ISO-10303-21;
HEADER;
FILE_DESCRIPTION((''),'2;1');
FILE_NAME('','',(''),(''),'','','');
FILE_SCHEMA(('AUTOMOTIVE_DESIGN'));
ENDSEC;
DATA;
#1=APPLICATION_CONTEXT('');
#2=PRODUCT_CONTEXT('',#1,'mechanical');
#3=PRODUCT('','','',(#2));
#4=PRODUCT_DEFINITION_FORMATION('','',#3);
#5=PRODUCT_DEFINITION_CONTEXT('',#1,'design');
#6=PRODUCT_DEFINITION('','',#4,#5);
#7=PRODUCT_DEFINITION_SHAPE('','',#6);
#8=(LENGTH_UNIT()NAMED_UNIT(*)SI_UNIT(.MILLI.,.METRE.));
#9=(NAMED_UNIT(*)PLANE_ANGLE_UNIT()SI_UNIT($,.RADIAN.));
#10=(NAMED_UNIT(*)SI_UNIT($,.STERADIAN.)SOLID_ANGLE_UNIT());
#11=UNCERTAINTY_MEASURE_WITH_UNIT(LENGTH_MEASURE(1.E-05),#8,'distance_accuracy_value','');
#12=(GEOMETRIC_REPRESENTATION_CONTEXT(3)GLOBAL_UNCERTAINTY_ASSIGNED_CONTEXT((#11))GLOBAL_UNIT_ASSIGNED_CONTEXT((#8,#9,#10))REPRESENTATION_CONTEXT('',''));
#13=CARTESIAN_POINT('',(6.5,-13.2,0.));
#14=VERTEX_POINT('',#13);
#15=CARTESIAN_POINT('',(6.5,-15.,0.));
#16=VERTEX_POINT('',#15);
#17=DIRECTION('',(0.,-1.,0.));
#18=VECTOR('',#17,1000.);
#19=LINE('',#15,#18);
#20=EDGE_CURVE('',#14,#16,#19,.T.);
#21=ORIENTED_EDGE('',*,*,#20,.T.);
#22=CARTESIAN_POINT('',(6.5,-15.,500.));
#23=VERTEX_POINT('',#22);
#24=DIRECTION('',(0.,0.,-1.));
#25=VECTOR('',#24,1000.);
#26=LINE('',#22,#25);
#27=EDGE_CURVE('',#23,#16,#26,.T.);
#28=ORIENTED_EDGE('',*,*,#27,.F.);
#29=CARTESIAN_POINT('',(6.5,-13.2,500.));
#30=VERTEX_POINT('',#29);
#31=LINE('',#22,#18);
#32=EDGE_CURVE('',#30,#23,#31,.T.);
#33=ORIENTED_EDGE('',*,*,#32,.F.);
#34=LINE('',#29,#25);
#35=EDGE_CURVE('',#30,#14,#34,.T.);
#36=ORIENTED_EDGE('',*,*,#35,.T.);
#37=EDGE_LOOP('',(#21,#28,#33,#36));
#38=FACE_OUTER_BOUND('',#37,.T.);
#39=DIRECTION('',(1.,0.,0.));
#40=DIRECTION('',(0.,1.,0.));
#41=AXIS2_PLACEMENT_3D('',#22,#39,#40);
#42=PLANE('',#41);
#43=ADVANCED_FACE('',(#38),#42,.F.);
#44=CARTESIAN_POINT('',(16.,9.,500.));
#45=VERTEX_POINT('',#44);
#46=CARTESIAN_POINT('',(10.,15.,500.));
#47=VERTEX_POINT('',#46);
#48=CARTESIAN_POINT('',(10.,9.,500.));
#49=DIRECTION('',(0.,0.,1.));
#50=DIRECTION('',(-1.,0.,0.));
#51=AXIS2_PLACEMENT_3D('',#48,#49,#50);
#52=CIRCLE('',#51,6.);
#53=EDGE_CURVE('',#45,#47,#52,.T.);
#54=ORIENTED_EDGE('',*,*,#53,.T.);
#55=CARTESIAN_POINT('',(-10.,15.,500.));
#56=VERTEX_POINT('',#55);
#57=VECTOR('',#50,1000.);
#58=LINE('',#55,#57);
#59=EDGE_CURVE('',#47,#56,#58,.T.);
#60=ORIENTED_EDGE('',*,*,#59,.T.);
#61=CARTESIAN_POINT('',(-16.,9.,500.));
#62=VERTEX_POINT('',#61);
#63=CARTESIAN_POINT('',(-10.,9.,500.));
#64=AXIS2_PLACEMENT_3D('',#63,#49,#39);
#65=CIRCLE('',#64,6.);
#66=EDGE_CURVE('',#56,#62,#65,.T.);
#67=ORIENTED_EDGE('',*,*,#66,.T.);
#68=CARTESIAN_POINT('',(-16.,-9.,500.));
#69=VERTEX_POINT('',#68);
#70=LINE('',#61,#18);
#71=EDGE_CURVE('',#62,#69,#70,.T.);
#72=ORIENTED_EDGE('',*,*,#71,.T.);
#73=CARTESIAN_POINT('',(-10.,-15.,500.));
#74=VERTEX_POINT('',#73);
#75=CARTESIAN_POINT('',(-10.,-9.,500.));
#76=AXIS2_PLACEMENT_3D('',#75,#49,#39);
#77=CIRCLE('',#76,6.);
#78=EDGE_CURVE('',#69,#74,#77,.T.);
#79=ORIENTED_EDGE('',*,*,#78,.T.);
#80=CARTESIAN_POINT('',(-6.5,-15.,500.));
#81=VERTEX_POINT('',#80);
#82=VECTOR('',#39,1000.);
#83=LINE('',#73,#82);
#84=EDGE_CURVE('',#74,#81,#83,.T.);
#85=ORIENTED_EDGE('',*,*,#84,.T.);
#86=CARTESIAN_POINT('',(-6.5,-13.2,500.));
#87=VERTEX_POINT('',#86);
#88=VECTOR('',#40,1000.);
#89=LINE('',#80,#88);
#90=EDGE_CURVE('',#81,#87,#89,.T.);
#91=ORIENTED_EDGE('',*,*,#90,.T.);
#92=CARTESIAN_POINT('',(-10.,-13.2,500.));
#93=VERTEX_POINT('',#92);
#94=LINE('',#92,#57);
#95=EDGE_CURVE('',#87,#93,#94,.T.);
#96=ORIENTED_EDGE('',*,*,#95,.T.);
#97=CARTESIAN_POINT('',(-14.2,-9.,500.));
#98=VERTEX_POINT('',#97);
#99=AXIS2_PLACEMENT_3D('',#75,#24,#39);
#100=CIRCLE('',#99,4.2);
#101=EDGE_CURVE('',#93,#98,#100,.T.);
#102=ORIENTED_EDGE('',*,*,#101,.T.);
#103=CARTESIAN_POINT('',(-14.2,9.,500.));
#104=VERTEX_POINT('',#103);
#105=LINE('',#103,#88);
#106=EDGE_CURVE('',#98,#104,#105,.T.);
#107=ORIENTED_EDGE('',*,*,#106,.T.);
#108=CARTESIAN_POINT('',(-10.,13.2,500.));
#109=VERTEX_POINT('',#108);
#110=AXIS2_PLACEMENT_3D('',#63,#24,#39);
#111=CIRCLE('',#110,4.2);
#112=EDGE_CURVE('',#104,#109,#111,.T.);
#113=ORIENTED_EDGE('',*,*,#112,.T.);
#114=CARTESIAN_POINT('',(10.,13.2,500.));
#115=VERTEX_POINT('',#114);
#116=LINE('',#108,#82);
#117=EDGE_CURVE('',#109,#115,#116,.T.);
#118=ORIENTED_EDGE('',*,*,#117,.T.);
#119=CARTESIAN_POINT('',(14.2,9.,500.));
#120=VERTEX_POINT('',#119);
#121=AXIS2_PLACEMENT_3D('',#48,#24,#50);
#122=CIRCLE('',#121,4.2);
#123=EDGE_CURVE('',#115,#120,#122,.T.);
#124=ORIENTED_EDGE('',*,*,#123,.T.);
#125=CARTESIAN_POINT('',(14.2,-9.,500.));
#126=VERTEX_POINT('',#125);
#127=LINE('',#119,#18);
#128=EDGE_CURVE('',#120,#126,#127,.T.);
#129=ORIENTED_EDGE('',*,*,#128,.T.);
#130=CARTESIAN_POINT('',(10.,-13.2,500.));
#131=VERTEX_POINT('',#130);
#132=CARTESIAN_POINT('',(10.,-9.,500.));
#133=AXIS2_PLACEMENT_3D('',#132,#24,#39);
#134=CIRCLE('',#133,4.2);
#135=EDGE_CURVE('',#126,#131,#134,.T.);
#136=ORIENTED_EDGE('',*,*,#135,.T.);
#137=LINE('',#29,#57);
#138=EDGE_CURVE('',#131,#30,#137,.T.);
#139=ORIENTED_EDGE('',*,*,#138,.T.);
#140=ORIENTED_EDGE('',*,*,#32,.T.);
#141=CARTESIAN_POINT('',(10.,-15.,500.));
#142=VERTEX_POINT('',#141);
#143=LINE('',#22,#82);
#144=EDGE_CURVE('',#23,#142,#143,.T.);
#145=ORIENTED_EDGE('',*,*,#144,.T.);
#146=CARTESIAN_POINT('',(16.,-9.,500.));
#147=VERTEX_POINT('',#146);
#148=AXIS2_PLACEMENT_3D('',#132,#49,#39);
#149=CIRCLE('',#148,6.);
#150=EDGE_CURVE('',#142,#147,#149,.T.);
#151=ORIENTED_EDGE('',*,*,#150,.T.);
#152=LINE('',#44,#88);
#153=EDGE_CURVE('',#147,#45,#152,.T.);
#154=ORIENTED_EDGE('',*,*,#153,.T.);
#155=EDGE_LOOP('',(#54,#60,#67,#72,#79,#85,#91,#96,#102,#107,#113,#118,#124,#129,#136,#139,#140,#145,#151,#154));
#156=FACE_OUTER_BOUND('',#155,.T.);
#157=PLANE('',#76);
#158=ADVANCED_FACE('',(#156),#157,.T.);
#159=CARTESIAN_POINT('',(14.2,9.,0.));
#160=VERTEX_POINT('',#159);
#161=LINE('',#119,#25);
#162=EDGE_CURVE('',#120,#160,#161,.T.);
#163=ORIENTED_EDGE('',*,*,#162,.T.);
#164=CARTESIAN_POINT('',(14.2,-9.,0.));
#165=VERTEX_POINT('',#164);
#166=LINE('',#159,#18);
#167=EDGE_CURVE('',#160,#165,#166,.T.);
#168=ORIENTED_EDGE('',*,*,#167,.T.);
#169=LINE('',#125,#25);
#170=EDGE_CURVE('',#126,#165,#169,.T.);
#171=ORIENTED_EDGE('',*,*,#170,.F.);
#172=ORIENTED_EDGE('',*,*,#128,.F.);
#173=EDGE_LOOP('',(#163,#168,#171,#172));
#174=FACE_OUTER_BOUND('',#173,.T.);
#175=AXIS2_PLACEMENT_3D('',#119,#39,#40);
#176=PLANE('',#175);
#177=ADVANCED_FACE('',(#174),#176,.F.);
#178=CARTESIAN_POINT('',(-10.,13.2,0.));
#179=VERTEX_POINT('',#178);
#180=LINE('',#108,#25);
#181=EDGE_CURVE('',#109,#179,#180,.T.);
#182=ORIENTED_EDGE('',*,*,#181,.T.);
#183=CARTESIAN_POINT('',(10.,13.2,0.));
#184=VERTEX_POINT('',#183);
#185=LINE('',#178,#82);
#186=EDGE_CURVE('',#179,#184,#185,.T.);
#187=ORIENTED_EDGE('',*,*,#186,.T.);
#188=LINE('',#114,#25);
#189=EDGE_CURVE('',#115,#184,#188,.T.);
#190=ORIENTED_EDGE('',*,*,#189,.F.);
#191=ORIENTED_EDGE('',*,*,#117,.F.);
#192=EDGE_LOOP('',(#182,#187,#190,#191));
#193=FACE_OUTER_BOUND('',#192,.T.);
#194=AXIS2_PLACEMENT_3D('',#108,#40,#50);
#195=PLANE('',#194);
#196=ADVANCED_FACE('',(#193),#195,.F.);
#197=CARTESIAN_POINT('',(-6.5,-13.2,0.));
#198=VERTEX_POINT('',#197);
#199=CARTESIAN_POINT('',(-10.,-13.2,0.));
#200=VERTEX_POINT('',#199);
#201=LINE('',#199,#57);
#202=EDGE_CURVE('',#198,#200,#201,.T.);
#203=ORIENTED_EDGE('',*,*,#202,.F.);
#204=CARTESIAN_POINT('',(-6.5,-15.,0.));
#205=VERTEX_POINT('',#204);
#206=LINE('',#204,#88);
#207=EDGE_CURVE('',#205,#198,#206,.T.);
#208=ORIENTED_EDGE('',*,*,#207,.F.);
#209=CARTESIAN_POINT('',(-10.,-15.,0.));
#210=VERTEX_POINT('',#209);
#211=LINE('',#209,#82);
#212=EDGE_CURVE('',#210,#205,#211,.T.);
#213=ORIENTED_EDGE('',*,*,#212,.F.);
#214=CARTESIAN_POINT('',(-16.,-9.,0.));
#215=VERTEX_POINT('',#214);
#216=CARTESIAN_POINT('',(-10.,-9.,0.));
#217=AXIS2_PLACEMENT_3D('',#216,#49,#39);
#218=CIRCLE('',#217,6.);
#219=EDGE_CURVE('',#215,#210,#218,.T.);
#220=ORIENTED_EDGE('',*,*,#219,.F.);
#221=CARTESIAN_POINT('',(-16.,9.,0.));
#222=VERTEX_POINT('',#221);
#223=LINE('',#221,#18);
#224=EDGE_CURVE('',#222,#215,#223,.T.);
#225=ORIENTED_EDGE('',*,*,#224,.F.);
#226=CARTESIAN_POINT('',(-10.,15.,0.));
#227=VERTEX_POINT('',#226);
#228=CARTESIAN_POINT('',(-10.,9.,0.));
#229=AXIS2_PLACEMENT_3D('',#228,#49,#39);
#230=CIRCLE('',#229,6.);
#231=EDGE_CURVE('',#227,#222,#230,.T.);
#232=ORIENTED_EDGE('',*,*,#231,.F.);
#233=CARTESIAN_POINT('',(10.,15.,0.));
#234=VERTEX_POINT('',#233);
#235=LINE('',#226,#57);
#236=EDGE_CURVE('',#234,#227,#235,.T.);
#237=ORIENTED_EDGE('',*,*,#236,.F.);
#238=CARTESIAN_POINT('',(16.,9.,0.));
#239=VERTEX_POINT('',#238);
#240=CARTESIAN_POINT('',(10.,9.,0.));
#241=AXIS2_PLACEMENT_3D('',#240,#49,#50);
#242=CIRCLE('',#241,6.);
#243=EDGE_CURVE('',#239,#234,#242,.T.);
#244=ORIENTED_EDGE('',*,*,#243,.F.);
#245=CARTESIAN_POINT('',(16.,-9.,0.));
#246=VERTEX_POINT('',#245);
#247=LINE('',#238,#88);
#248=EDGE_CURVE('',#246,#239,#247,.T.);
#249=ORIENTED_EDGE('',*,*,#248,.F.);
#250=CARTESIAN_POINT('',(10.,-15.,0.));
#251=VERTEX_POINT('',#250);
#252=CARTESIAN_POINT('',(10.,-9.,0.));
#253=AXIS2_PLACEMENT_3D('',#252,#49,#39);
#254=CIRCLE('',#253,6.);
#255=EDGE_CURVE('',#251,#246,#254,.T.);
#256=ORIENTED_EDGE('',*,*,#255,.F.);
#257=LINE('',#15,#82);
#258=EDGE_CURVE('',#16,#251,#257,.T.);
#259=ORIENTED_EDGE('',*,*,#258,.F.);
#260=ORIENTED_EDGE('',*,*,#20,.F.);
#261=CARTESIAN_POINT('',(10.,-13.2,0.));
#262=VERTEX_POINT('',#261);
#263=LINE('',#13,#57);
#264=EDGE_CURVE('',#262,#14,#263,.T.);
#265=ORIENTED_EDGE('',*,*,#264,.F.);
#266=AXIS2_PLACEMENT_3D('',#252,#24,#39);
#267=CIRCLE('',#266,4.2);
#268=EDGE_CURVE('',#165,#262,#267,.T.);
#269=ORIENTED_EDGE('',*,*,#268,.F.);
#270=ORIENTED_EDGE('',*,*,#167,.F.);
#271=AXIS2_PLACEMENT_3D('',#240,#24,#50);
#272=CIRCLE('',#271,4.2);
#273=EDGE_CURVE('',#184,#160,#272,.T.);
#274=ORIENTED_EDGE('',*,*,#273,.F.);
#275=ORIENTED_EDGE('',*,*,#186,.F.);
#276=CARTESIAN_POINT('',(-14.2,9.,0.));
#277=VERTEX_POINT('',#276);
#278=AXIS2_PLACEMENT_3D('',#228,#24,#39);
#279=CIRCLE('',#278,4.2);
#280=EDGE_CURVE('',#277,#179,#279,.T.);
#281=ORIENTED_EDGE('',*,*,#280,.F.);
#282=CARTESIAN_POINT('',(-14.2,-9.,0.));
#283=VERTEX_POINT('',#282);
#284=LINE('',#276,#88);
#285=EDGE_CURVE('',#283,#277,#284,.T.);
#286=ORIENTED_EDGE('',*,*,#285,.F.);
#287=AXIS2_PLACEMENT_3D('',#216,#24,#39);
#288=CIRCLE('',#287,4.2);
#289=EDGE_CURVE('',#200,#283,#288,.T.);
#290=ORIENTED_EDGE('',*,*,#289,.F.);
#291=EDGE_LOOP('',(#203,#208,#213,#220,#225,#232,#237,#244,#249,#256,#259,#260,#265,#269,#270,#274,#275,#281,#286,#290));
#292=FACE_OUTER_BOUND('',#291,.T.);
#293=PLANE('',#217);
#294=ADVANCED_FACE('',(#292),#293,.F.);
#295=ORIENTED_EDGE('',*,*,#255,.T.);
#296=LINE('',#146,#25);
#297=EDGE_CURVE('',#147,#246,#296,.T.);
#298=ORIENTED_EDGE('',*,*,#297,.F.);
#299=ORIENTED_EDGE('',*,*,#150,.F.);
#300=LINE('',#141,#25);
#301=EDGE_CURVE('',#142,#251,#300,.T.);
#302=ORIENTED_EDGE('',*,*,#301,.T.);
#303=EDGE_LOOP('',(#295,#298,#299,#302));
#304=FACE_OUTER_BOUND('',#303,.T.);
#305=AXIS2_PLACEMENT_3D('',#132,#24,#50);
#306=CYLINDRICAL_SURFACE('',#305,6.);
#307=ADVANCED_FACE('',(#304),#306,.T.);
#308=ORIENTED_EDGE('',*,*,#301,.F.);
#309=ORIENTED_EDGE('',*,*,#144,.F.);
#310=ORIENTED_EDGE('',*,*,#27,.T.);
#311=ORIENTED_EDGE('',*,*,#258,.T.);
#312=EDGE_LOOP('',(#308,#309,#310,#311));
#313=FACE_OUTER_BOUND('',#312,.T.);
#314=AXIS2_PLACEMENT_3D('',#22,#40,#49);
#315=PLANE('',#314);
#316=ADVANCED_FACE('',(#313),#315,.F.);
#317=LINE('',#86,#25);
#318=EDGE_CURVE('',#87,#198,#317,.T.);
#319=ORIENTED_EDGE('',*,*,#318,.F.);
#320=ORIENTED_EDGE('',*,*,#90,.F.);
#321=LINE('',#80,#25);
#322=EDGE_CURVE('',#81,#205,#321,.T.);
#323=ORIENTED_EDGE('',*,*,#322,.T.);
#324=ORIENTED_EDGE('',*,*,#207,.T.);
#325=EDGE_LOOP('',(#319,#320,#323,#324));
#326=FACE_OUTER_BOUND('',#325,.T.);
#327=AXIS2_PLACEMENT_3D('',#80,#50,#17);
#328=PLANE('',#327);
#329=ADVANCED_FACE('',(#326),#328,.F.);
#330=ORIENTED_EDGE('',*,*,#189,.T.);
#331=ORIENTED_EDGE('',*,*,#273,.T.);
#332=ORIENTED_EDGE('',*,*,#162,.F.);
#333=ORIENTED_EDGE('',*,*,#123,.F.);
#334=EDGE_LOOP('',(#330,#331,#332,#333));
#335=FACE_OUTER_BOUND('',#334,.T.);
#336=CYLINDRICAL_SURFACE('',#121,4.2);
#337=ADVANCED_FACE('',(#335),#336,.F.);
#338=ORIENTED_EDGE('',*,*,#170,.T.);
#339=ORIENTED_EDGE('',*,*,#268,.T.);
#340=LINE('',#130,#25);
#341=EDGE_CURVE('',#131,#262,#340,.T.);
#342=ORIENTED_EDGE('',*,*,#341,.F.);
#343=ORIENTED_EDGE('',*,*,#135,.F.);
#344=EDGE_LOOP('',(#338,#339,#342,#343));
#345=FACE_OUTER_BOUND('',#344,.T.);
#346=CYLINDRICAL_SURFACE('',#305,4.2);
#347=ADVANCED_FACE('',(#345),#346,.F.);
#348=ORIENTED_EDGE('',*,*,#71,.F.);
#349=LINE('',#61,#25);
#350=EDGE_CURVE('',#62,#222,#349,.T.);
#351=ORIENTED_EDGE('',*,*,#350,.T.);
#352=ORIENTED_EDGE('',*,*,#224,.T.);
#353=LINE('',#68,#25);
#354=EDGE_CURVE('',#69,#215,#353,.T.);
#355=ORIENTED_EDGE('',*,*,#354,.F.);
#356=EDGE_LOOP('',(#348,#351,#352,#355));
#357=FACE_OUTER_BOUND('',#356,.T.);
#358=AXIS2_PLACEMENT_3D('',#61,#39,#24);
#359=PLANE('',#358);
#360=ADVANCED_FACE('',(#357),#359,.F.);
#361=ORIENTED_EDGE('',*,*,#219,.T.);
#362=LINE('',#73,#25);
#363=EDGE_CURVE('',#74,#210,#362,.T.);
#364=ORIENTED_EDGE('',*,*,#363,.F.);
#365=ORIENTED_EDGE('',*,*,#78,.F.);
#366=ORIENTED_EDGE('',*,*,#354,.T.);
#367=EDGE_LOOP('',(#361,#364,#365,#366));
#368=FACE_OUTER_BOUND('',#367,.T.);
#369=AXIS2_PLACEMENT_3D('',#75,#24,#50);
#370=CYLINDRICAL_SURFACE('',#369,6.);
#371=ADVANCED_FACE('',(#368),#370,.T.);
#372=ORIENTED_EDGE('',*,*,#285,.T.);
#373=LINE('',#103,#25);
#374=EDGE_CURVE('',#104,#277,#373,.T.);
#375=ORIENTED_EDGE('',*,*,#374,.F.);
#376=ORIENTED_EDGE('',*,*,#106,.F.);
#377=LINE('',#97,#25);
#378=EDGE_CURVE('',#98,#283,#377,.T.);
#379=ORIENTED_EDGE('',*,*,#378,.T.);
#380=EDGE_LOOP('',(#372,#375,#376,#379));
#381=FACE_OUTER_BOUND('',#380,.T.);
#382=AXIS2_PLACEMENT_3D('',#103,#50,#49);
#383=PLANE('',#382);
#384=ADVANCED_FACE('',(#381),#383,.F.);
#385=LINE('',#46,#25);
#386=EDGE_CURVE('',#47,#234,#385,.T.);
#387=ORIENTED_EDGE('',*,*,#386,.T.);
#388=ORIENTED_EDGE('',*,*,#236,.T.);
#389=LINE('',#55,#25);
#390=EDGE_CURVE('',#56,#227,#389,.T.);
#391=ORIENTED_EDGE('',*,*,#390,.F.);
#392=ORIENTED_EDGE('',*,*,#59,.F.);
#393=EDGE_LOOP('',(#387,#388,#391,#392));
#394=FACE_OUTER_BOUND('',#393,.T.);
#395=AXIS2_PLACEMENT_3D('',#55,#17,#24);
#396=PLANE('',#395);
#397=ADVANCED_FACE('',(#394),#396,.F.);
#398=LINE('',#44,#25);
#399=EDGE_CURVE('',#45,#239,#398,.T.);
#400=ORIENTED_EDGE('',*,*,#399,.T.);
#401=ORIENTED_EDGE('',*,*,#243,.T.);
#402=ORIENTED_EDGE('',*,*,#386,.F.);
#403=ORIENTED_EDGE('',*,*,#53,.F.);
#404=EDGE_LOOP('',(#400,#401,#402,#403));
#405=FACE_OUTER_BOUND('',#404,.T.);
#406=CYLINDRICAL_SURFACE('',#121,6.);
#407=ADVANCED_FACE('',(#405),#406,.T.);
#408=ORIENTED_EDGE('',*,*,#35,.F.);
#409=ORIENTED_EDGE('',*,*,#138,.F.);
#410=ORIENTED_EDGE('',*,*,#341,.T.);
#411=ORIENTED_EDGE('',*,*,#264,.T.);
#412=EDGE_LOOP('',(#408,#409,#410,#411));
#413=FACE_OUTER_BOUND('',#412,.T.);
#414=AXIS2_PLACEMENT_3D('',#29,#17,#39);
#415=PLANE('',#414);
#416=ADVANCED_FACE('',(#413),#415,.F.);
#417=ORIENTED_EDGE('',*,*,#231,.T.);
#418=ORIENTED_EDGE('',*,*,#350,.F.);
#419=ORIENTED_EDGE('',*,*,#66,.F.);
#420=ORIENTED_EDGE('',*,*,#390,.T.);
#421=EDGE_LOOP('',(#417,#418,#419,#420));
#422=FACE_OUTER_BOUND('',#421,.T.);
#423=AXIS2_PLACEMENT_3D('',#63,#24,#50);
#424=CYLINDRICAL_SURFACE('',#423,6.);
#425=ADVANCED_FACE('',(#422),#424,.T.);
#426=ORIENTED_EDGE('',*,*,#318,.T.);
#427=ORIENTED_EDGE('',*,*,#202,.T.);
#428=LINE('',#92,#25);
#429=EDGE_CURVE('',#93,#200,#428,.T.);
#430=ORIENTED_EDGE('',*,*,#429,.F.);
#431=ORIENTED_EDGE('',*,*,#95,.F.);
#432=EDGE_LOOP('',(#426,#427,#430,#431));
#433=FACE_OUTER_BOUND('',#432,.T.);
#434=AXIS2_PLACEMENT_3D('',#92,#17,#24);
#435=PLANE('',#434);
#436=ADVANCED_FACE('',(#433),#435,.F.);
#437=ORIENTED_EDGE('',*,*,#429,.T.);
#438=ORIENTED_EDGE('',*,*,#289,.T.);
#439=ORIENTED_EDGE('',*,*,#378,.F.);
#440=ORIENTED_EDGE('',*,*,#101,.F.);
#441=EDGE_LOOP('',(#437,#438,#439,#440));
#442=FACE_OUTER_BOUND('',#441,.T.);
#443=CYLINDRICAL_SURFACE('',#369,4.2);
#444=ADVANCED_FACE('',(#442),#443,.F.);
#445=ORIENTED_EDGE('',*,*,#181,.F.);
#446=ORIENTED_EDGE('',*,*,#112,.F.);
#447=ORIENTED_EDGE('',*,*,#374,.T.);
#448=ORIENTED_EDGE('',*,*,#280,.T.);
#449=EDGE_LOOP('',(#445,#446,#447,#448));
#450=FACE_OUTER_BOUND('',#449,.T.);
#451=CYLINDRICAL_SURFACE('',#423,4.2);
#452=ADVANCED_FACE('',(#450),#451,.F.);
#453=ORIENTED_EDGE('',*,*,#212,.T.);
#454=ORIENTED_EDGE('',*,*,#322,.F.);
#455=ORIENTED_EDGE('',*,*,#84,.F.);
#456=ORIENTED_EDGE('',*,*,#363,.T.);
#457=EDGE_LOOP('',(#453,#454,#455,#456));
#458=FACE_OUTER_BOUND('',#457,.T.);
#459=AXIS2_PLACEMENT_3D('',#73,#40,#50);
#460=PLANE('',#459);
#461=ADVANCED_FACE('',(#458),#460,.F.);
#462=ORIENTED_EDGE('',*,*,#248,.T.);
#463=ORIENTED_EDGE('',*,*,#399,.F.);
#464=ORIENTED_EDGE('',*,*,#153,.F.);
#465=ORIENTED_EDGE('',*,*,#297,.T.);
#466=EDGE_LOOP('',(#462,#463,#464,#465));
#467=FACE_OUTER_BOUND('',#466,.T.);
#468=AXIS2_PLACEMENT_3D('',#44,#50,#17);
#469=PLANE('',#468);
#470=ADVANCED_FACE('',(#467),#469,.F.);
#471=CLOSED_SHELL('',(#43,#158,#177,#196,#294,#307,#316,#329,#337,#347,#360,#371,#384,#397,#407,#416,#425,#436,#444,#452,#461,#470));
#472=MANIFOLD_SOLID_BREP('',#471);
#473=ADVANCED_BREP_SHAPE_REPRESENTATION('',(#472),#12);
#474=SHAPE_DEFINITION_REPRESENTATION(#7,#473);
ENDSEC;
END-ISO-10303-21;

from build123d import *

# Parameters (mm, degrees)
BOSS_EXTRUDE1_DEPTH = 500


with BuildPart() as part:
    # Sketch1 → Boss-Extrude1 (new body)
    with BuildSketch(Plane.XY):
        with BuildLine():
            Line((-10, -13.2), (-6.5, -13.2))
            Line((-6.5, -13.2), (-6.5, -15))
            Line((-6.5, -15), (-10, -15))
            ThreePointArc((-10, -15), (-14.242640687, -13.242640687), (-16, -9))
            Line((-16, -9), (-16, 9))
            ThreePointArc((-16, 9), (-14.242640687, 13.242640687), (-10, 15))
            Line((-10, 15), (10, 15))
            ThreePointArc((10, 15), (14.242640687, 13.242640687), (16, 9))
            Line((16, 9), (16, -9))
            ThreePointArc((16, -9), (14.242640687, -13.242640687), (10, -15))
            Line((10, -15), (6.5, -15))
            Line((6.5, -15), (6.5, -13.2))
            Line((6.5, -13.2), (10, -13.2))
            ThreePointArc((10, -13.2), (12.969848481, -11.969848481), (14.2, -9))
            Line((14.2, -9), (14.2, 9))
            ThreePointArc((14.2, 9), (12.969848481, 11.969848481), (10, 13.2))
            Line((10, 13.2), (-10, 13.2))
            ThreePointArc((-10, 13.2), (-12.969848481, 11.969848481), (-14.2, 9))
            Line((-14.2, 9), (-14.2, -9))
            ThreePointArc((-14.2, -9), (-12.969848481, -11.969848481), (-10, -13.2))
        make_face()
    extrude(amount=BOSS_EXTRUDE1_DEPTH)


solid = part.part
